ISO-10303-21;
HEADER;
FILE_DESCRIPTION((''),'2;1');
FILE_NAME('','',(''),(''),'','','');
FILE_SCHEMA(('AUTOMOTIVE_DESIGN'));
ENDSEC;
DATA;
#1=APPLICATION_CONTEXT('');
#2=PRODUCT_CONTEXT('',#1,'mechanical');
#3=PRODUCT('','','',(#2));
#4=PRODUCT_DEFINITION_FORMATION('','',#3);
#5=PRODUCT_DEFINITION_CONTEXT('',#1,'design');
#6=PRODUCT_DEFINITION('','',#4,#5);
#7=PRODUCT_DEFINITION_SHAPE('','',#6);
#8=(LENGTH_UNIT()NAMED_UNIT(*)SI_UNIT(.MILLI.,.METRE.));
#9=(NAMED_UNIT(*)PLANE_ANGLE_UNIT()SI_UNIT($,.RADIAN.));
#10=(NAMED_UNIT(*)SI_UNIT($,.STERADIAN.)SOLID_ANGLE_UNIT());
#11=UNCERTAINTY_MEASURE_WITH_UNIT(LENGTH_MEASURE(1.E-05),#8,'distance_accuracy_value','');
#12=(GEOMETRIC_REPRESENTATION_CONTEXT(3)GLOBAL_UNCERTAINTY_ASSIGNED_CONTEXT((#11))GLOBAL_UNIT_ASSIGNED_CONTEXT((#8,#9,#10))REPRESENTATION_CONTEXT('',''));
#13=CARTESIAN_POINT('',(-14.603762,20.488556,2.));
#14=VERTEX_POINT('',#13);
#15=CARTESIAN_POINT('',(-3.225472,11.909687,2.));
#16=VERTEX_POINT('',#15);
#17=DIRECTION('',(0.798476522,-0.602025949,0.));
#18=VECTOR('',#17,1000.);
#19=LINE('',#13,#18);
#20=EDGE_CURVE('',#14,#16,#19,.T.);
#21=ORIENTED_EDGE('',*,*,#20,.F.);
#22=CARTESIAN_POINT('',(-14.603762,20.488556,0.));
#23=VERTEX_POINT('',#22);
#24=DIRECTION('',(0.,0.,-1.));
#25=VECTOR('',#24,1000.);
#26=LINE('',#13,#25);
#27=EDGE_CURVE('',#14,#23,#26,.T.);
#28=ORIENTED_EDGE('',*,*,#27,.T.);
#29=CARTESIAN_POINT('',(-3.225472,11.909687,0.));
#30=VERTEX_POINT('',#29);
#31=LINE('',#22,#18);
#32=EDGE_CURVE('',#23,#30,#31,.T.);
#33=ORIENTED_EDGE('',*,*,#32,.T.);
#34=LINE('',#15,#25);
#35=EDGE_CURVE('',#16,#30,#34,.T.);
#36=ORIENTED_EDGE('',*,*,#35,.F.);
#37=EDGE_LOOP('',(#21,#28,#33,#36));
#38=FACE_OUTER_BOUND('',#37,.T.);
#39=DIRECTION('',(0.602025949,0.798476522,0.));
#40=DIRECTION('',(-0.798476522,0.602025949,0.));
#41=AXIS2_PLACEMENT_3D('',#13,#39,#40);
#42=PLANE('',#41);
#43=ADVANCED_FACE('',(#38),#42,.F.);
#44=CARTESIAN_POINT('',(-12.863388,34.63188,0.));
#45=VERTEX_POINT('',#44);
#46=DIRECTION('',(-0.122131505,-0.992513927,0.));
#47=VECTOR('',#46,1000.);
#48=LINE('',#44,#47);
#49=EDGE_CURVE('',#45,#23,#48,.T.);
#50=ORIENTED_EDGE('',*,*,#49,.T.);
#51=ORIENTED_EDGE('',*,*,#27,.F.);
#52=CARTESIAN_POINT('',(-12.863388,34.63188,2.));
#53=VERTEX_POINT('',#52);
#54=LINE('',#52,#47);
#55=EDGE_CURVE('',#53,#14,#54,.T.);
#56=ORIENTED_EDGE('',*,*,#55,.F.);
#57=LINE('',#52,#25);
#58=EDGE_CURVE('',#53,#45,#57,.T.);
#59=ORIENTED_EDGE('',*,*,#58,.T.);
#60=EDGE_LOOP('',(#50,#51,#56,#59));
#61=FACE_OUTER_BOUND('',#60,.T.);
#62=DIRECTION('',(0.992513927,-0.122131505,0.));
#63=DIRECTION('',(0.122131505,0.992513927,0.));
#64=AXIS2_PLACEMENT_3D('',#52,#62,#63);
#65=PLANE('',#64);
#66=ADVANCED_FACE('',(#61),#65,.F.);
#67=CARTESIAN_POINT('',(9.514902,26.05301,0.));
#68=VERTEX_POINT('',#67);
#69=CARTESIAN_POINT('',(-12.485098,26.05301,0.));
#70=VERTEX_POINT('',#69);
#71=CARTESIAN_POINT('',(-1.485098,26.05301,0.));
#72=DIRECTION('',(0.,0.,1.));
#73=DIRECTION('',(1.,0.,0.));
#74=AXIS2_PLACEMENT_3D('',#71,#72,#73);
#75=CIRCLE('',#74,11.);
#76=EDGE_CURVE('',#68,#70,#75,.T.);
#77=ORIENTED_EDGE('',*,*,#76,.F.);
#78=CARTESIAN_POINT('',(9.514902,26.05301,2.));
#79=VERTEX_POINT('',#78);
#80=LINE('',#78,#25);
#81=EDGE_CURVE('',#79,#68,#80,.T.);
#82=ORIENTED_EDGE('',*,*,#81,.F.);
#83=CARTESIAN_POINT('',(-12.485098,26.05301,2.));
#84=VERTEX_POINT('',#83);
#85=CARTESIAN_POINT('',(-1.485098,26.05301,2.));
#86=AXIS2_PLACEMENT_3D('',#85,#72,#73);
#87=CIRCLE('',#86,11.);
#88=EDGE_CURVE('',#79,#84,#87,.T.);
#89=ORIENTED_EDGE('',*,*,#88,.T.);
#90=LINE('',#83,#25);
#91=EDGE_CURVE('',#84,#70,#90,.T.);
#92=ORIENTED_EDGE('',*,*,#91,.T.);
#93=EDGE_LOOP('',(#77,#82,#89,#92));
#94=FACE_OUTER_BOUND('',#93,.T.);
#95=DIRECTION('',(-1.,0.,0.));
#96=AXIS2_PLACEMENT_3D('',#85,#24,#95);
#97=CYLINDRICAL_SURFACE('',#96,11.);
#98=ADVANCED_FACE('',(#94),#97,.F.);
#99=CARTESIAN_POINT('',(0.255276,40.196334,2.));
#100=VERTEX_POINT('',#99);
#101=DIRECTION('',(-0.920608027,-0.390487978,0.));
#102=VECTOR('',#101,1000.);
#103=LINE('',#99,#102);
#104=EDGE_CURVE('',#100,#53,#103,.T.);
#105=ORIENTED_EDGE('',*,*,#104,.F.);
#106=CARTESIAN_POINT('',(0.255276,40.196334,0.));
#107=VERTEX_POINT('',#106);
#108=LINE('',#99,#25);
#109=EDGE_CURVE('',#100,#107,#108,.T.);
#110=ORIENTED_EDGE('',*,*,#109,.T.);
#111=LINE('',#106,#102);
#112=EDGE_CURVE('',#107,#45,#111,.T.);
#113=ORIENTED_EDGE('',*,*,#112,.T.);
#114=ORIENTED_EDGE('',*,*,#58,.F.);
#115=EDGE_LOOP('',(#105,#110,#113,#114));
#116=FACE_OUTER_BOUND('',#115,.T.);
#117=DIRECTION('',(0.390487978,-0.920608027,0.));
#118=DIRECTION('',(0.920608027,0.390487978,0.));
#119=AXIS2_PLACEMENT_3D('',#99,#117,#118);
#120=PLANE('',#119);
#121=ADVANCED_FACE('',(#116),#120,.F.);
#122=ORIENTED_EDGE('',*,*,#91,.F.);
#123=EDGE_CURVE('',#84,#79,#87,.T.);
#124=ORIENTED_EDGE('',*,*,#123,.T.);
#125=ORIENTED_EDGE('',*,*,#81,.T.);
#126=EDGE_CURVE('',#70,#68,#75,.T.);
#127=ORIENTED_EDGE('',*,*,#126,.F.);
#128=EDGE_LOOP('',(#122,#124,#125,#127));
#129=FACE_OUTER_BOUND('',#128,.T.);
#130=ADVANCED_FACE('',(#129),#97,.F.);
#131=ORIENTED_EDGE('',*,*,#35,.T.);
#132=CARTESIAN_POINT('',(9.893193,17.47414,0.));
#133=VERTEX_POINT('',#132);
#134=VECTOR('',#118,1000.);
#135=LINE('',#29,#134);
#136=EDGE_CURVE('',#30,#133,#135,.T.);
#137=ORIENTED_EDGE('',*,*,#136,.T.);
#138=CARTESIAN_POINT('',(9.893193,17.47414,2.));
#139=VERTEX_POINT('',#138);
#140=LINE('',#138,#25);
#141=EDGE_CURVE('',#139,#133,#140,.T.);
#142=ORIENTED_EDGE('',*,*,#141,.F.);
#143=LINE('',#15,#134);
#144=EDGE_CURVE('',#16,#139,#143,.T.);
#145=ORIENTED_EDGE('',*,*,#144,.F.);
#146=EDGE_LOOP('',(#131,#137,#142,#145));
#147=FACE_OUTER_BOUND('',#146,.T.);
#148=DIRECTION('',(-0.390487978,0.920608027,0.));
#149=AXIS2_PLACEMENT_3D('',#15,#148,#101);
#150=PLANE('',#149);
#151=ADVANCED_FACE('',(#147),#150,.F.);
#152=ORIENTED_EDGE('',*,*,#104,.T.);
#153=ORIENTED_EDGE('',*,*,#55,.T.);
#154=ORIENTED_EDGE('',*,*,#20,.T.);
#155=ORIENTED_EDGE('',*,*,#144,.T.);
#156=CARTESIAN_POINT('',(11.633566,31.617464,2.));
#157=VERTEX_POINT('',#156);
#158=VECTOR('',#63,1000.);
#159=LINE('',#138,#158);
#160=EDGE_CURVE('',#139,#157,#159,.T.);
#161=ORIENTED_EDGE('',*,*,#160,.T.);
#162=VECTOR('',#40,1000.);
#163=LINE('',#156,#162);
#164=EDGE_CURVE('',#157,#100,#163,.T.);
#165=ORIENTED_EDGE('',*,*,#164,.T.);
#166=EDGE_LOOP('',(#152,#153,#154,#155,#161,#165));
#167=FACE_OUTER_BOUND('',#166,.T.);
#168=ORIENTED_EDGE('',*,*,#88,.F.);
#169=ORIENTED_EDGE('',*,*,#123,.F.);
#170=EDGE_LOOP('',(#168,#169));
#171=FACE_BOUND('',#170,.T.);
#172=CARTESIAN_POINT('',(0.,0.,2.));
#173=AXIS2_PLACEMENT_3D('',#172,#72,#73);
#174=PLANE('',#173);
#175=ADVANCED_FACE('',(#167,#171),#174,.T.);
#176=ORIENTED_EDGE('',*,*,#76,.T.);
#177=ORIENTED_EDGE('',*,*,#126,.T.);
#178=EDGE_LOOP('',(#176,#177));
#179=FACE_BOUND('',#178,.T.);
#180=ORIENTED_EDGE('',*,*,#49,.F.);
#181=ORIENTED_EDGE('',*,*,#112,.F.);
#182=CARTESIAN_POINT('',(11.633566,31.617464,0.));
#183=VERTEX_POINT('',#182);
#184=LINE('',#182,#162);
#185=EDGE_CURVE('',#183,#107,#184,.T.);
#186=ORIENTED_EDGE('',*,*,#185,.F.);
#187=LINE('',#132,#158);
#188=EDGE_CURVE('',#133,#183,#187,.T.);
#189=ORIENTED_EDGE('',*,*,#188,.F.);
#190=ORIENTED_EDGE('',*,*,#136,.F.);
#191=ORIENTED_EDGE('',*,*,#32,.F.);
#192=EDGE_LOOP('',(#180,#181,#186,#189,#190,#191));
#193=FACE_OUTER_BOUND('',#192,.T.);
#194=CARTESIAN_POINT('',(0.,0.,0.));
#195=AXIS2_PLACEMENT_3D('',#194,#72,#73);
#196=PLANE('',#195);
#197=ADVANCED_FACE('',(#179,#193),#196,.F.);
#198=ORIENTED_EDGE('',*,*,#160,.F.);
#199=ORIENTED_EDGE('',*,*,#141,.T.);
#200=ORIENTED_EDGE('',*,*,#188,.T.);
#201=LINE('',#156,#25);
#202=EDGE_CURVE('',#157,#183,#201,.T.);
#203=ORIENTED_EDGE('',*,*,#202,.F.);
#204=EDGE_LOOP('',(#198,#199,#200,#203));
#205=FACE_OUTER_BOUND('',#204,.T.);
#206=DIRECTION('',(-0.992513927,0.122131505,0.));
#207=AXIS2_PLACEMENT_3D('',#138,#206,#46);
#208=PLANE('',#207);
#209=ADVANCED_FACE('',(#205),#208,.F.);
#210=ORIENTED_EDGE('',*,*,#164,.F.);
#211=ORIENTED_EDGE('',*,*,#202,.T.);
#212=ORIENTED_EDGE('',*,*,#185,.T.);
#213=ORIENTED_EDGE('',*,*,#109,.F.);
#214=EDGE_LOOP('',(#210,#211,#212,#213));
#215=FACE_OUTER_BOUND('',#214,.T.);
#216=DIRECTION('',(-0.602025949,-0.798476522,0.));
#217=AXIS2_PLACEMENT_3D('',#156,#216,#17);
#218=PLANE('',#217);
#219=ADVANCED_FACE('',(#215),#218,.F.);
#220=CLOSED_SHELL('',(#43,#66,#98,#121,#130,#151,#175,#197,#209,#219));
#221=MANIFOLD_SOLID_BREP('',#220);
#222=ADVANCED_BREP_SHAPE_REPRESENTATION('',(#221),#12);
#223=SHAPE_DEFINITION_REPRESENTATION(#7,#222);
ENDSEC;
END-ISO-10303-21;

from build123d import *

# Parameters (mm, degrees)
SKETCH_1_R      = 11
EXTRUDE_1_DEPTH = 2


with BuildPart() as part:
    # 草图1 → 凸台-拉伸1 (new body)
    with BuildSketch(Plane.XY):
        Polygon((9.893192504, 17.474140349), (11.633566446, 31.61746381), (0.255276005, 40.196333587), (-12.863388378, 34.631879902), (-14.60376232, 20.48855644), (-3.225471879, 11.909686664), align=None)
        with Locations((-1.485097937, 26.053010125)):
            Circle(SKETCH_1_R, mode=Mode.SUBTRACT)
    extrude(amount=EXTRUDE_1_DEPTH)


solid = part.part
